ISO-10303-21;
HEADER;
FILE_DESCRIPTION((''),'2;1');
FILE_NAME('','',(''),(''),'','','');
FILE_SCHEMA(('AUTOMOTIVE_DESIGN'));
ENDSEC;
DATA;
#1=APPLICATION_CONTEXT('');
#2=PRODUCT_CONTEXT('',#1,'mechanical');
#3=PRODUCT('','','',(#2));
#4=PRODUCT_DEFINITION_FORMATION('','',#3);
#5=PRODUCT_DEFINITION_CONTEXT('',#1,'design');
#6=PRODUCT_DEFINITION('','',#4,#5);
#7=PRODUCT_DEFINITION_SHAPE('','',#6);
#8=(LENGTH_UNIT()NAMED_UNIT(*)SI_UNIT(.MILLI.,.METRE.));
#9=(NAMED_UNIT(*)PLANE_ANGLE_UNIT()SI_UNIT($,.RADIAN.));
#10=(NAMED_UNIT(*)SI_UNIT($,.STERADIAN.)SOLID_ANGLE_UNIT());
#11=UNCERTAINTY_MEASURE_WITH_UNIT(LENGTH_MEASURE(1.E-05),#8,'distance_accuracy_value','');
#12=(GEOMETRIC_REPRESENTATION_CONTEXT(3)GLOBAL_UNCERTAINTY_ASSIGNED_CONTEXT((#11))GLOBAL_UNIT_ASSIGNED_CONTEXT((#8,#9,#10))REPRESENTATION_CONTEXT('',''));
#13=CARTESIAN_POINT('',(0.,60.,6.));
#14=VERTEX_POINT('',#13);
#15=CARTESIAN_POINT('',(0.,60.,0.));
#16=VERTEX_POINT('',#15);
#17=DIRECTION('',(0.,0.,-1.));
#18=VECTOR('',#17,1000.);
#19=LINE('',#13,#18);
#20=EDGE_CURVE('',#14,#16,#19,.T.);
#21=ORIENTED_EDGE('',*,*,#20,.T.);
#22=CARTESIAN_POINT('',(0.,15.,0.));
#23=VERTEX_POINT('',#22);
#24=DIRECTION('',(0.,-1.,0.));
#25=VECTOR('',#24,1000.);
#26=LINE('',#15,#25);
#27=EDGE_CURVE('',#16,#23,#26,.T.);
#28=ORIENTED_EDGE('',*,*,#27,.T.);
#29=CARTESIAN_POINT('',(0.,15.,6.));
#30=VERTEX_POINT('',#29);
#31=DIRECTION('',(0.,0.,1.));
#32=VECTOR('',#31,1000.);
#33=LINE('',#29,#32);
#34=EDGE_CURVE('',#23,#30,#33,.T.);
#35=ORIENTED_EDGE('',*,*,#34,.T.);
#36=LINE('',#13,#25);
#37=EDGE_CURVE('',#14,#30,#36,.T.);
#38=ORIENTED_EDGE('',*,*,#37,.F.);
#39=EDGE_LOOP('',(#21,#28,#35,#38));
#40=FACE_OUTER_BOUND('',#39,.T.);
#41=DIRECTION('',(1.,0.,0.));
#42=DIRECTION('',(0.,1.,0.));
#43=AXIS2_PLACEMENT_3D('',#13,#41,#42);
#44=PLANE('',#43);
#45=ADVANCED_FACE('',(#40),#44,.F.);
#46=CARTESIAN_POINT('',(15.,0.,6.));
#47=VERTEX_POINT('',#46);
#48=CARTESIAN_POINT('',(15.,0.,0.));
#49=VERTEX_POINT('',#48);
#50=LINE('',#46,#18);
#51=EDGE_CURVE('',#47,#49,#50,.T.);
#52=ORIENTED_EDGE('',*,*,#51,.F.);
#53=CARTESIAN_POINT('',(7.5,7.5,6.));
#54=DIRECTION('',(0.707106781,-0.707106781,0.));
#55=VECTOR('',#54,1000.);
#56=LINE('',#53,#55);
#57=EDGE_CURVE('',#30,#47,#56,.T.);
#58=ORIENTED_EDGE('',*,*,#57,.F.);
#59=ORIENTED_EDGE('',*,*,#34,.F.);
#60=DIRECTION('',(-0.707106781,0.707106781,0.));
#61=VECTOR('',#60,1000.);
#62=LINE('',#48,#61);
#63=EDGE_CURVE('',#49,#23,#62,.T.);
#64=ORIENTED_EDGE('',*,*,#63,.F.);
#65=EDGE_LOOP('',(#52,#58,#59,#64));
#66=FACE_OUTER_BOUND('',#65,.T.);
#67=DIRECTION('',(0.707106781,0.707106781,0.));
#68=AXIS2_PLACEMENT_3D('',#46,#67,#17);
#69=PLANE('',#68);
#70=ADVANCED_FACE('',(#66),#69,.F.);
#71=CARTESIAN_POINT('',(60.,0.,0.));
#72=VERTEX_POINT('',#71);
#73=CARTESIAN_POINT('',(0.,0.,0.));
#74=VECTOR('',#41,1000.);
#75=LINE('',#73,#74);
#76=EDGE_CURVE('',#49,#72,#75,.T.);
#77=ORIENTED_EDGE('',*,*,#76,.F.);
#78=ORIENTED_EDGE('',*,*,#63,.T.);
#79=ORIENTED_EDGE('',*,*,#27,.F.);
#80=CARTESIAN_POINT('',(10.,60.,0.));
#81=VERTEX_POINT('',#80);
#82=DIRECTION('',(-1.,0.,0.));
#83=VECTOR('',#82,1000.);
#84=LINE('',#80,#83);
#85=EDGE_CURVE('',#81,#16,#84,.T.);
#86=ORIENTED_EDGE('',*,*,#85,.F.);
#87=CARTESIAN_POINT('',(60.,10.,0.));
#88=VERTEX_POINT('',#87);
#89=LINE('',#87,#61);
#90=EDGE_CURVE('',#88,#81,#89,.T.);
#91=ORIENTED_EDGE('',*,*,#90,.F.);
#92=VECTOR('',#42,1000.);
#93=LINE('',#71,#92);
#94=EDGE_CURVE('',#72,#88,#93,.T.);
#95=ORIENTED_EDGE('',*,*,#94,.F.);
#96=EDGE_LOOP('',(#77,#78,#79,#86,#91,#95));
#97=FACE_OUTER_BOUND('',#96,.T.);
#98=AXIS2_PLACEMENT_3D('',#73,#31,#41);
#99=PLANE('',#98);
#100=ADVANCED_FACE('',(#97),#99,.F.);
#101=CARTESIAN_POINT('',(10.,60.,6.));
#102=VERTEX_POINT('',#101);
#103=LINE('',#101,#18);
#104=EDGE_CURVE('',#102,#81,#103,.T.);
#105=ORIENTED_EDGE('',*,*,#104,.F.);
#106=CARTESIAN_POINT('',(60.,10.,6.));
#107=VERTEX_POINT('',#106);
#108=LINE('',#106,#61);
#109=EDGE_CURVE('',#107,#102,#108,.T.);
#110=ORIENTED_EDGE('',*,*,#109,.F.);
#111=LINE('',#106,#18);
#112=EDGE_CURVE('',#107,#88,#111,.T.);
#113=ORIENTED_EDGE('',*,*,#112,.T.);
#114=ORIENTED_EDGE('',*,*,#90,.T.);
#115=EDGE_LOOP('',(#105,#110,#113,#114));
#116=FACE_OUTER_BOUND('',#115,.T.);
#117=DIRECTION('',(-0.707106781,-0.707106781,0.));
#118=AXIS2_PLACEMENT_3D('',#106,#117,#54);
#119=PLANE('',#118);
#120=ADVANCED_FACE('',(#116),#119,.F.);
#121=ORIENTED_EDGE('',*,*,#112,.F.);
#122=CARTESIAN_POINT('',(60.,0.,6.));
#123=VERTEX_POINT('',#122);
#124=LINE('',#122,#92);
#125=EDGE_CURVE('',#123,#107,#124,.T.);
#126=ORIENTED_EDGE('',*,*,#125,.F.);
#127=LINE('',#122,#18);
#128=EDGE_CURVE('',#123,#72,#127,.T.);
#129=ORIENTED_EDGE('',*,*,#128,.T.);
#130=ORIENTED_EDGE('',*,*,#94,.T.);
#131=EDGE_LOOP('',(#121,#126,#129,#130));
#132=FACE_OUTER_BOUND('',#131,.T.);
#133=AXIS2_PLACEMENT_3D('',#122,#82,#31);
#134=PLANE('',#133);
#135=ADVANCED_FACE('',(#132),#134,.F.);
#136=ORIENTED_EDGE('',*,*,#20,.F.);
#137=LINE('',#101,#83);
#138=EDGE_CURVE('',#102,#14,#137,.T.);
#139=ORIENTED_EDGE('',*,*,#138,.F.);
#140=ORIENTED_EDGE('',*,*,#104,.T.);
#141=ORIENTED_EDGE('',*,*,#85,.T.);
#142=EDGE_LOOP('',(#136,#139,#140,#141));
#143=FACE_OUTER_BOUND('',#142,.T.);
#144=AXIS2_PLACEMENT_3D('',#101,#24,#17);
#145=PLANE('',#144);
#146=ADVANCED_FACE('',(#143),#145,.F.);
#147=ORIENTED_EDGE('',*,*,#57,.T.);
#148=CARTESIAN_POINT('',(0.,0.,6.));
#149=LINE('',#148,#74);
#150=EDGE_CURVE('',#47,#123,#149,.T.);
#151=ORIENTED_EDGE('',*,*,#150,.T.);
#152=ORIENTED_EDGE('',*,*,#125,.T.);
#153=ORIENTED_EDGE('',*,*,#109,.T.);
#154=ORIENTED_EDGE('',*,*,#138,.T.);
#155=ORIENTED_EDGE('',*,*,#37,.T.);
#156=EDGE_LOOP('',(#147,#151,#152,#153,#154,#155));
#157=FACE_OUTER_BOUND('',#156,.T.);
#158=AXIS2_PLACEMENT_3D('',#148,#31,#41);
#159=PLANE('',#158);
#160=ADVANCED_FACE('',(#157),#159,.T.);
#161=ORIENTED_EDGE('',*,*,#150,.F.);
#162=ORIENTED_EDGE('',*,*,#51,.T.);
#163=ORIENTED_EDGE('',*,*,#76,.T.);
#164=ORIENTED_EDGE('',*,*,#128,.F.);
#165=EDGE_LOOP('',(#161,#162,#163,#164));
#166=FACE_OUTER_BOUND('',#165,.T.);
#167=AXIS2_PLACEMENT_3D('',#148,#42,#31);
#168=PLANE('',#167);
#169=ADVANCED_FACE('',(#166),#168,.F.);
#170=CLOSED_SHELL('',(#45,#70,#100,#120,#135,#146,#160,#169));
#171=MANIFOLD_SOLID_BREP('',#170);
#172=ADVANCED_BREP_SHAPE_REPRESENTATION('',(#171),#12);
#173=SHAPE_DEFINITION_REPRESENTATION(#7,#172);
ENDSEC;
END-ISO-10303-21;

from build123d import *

# Parameters (mm, degrees)
BOSS_EXTRUDE1_DEPTH = 6
CHAMFER1_SIZE       = 15


with BuildPart() as part:
    # Sketch1 → Boss-Extrude1 (new body)
    with BuildSketch(Plane.XY):
        Polygon((0, 60), (0, 0), (60, 0), (60, 10), (10, 60), align=None)
    extrude(amount=BOSS_EXTRUDE1_DEPTH)

    # Chamfer1
    chamfer1_edges = [part.edges().sort_by_distance(p)[0] for p in [
        (0, 0, 3),
    ]]
    chamfer(chamfer1_edges, length=CHAMFER1_SIZE)


solid = part.part
